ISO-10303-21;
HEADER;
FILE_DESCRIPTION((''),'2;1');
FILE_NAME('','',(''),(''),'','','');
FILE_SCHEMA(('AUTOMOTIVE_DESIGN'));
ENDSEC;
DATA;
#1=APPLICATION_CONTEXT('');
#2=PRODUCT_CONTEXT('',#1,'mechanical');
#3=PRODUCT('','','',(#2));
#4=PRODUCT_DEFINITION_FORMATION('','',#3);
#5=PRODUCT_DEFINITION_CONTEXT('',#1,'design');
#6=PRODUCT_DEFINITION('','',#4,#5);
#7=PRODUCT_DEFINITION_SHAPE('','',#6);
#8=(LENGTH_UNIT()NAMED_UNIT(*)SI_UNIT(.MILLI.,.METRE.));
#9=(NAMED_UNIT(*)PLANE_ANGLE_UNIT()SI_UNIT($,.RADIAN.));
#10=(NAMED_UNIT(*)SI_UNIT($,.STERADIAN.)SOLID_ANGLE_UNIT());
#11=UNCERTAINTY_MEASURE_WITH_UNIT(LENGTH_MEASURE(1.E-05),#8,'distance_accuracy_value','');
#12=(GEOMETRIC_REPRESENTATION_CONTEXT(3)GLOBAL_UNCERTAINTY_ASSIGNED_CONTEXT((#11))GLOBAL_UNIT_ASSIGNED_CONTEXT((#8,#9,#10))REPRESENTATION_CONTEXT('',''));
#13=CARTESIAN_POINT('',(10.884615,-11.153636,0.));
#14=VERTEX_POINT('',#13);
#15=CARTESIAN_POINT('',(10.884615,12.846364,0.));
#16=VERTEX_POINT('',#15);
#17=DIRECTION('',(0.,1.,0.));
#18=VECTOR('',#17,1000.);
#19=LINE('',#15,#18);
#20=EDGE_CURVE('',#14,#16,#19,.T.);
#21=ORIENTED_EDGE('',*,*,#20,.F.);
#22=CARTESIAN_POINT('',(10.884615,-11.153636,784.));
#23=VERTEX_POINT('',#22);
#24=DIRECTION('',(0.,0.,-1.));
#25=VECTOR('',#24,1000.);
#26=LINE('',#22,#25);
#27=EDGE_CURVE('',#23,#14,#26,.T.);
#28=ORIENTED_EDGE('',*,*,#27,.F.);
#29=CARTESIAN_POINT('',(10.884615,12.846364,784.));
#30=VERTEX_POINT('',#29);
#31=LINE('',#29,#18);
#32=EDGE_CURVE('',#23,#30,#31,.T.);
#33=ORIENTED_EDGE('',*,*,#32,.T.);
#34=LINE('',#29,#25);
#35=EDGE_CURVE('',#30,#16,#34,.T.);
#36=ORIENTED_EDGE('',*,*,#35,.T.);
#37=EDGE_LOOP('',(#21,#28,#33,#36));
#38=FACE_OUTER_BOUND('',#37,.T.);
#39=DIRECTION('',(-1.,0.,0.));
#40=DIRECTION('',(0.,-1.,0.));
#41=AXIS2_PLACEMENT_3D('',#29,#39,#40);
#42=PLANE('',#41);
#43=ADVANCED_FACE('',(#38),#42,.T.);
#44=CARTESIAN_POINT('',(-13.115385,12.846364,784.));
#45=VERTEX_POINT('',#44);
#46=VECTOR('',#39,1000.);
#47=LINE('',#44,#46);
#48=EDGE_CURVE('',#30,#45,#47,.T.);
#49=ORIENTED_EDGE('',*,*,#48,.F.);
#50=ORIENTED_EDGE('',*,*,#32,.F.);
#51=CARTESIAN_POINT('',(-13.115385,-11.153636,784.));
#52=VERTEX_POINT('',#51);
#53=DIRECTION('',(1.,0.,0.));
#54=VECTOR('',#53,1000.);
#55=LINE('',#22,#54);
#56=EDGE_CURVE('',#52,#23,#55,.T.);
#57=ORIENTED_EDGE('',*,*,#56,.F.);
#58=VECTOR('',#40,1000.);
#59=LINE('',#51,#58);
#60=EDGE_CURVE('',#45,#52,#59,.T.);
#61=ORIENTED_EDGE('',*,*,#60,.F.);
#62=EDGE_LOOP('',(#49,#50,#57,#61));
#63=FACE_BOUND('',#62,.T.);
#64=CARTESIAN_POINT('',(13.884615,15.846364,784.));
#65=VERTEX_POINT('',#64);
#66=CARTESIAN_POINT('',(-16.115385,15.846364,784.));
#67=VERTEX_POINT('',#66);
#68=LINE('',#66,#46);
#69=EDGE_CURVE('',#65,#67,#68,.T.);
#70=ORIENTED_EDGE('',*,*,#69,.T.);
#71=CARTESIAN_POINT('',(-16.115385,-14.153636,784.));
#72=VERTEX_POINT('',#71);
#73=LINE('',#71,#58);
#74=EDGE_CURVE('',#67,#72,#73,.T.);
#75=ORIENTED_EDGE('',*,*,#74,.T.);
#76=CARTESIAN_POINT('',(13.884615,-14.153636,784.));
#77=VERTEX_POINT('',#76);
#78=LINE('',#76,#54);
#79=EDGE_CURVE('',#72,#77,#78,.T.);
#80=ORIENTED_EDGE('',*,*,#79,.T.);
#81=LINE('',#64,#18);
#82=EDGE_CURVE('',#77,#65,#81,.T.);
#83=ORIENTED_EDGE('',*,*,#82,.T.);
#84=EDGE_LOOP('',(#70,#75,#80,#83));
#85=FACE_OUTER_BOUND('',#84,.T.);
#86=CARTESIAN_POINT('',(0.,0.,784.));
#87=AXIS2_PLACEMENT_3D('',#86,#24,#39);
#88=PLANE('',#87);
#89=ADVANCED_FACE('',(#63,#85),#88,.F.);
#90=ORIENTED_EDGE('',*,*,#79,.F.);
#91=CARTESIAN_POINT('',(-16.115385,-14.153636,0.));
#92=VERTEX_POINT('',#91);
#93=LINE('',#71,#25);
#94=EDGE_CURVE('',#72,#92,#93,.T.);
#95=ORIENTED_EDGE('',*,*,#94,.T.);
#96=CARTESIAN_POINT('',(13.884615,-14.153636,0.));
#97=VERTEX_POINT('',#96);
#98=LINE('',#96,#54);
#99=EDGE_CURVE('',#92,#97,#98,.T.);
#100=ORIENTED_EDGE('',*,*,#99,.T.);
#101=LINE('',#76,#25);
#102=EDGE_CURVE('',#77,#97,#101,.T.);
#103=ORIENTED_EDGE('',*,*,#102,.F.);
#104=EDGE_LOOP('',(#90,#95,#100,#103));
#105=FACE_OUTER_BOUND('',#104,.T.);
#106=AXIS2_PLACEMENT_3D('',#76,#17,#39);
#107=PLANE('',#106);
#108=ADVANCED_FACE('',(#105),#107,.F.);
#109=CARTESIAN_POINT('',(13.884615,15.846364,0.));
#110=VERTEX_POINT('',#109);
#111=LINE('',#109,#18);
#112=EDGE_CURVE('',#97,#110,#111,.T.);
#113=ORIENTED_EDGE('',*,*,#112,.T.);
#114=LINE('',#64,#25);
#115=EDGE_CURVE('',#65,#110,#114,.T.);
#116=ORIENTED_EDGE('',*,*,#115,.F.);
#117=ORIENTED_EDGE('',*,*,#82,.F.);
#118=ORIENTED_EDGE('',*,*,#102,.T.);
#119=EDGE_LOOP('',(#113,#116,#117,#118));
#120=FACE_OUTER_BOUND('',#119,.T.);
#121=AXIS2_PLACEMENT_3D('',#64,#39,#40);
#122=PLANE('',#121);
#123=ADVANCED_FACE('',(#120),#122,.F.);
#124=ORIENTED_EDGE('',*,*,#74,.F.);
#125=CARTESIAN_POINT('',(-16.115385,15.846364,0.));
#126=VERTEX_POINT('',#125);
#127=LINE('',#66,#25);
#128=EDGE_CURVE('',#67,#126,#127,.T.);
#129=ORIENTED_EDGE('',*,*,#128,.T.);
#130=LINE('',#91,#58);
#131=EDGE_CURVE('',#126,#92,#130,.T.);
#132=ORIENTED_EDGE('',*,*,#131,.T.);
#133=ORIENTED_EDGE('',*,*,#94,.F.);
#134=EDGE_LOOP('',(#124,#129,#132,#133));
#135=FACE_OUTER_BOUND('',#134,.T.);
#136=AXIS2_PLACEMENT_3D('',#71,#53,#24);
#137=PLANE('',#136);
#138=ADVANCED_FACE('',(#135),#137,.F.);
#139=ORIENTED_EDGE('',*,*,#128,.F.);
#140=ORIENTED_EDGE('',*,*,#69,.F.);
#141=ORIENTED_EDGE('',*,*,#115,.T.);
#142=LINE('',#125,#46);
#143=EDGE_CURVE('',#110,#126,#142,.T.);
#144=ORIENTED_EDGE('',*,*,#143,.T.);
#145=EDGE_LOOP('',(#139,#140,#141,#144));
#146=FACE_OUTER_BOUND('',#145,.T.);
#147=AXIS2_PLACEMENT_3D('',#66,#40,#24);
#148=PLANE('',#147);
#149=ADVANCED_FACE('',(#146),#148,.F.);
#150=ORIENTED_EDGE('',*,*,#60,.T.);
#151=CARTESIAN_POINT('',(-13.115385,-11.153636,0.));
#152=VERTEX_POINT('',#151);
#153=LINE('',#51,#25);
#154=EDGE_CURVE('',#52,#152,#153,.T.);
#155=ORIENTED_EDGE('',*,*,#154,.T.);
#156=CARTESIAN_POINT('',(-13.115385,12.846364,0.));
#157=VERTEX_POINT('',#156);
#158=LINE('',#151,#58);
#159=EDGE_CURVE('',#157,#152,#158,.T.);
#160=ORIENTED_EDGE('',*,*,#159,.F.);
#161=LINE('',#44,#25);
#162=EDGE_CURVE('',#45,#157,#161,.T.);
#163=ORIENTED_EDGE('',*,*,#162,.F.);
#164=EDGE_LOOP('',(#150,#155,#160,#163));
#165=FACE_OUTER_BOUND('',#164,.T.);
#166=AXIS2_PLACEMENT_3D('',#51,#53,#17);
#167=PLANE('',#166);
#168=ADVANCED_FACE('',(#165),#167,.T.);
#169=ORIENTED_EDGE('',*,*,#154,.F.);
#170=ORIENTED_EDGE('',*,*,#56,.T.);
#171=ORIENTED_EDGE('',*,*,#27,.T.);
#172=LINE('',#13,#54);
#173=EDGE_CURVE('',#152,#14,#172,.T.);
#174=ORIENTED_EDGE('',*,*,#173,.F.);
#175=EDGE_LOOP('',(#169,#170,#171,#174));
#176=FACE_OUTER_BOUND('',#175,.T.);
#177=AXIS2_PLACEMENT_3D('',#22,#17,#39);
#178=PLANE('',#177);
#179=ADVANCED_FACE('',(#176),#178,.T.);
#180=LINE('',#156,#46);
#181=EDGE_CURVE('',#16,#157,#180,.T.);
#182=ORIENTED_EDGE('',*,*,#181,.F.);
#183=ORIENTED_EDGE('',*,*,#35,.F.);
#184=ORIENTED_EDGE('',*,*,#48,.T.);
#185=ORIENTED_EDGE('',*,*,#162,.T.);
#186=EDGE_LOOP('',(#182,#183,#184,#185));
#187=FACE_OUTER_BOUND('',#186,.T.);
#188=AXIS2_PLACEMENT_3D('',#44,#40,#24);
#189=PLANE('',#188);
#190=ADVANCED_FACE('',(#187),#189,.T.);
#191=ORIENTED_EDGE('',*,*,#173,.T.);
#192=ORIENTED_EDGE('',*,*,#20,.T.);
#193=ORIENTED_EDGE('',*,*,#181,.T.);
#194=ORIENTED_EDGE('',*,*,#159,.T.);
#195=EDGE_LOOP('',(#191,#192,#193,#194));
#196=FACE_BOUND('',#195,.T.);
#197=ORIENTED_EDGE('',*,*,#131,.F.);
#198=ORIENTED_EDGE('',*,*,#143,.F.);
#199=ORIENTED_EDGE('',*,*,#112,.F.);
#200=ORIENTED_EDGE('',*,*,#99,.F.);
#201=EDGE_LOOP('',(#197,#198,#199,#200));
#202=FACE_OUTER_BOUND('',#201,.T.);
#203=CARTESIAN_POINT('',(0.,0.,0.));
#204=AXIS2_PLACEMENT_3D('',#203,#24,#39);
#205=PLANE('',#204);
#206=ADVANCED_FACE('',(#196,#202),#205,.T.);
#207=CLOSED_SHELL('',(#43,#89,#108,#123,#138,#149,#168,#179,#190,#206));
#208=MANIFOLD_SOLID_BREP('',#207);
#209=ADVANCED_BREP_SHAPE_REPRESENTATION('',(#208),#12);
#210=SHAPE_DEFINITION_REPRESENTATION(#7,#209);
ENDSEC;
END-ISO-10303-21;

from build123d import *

# Parameters (mm, degrees)
SKETCH1_W           = 30
SKETCH1_H           = 30
SKETCH1_W_2         = 24
SKETCH1_H_2         = 24
BOSS_EXTRUDE2_DEPTH = 784


with BuildPart() as part:
    # Sketch1 → Boss-Extrude2 (new body)
    with BuildSketch(Plane.XY):
        with Locations((-1.115384615, 0.846363591)):
            Rectangle(SKETCH1_W, SKETCH1_H)
        with Locations((-1.115384615, 0.846363591)):
            Rectangle(SKETCH1_W_2, SKETCH1_H_2, mode=Mode.SUBTRACT)
    extrude(amount=BOSS_EXTRUDE2_DEPTH)


solid = part.part
